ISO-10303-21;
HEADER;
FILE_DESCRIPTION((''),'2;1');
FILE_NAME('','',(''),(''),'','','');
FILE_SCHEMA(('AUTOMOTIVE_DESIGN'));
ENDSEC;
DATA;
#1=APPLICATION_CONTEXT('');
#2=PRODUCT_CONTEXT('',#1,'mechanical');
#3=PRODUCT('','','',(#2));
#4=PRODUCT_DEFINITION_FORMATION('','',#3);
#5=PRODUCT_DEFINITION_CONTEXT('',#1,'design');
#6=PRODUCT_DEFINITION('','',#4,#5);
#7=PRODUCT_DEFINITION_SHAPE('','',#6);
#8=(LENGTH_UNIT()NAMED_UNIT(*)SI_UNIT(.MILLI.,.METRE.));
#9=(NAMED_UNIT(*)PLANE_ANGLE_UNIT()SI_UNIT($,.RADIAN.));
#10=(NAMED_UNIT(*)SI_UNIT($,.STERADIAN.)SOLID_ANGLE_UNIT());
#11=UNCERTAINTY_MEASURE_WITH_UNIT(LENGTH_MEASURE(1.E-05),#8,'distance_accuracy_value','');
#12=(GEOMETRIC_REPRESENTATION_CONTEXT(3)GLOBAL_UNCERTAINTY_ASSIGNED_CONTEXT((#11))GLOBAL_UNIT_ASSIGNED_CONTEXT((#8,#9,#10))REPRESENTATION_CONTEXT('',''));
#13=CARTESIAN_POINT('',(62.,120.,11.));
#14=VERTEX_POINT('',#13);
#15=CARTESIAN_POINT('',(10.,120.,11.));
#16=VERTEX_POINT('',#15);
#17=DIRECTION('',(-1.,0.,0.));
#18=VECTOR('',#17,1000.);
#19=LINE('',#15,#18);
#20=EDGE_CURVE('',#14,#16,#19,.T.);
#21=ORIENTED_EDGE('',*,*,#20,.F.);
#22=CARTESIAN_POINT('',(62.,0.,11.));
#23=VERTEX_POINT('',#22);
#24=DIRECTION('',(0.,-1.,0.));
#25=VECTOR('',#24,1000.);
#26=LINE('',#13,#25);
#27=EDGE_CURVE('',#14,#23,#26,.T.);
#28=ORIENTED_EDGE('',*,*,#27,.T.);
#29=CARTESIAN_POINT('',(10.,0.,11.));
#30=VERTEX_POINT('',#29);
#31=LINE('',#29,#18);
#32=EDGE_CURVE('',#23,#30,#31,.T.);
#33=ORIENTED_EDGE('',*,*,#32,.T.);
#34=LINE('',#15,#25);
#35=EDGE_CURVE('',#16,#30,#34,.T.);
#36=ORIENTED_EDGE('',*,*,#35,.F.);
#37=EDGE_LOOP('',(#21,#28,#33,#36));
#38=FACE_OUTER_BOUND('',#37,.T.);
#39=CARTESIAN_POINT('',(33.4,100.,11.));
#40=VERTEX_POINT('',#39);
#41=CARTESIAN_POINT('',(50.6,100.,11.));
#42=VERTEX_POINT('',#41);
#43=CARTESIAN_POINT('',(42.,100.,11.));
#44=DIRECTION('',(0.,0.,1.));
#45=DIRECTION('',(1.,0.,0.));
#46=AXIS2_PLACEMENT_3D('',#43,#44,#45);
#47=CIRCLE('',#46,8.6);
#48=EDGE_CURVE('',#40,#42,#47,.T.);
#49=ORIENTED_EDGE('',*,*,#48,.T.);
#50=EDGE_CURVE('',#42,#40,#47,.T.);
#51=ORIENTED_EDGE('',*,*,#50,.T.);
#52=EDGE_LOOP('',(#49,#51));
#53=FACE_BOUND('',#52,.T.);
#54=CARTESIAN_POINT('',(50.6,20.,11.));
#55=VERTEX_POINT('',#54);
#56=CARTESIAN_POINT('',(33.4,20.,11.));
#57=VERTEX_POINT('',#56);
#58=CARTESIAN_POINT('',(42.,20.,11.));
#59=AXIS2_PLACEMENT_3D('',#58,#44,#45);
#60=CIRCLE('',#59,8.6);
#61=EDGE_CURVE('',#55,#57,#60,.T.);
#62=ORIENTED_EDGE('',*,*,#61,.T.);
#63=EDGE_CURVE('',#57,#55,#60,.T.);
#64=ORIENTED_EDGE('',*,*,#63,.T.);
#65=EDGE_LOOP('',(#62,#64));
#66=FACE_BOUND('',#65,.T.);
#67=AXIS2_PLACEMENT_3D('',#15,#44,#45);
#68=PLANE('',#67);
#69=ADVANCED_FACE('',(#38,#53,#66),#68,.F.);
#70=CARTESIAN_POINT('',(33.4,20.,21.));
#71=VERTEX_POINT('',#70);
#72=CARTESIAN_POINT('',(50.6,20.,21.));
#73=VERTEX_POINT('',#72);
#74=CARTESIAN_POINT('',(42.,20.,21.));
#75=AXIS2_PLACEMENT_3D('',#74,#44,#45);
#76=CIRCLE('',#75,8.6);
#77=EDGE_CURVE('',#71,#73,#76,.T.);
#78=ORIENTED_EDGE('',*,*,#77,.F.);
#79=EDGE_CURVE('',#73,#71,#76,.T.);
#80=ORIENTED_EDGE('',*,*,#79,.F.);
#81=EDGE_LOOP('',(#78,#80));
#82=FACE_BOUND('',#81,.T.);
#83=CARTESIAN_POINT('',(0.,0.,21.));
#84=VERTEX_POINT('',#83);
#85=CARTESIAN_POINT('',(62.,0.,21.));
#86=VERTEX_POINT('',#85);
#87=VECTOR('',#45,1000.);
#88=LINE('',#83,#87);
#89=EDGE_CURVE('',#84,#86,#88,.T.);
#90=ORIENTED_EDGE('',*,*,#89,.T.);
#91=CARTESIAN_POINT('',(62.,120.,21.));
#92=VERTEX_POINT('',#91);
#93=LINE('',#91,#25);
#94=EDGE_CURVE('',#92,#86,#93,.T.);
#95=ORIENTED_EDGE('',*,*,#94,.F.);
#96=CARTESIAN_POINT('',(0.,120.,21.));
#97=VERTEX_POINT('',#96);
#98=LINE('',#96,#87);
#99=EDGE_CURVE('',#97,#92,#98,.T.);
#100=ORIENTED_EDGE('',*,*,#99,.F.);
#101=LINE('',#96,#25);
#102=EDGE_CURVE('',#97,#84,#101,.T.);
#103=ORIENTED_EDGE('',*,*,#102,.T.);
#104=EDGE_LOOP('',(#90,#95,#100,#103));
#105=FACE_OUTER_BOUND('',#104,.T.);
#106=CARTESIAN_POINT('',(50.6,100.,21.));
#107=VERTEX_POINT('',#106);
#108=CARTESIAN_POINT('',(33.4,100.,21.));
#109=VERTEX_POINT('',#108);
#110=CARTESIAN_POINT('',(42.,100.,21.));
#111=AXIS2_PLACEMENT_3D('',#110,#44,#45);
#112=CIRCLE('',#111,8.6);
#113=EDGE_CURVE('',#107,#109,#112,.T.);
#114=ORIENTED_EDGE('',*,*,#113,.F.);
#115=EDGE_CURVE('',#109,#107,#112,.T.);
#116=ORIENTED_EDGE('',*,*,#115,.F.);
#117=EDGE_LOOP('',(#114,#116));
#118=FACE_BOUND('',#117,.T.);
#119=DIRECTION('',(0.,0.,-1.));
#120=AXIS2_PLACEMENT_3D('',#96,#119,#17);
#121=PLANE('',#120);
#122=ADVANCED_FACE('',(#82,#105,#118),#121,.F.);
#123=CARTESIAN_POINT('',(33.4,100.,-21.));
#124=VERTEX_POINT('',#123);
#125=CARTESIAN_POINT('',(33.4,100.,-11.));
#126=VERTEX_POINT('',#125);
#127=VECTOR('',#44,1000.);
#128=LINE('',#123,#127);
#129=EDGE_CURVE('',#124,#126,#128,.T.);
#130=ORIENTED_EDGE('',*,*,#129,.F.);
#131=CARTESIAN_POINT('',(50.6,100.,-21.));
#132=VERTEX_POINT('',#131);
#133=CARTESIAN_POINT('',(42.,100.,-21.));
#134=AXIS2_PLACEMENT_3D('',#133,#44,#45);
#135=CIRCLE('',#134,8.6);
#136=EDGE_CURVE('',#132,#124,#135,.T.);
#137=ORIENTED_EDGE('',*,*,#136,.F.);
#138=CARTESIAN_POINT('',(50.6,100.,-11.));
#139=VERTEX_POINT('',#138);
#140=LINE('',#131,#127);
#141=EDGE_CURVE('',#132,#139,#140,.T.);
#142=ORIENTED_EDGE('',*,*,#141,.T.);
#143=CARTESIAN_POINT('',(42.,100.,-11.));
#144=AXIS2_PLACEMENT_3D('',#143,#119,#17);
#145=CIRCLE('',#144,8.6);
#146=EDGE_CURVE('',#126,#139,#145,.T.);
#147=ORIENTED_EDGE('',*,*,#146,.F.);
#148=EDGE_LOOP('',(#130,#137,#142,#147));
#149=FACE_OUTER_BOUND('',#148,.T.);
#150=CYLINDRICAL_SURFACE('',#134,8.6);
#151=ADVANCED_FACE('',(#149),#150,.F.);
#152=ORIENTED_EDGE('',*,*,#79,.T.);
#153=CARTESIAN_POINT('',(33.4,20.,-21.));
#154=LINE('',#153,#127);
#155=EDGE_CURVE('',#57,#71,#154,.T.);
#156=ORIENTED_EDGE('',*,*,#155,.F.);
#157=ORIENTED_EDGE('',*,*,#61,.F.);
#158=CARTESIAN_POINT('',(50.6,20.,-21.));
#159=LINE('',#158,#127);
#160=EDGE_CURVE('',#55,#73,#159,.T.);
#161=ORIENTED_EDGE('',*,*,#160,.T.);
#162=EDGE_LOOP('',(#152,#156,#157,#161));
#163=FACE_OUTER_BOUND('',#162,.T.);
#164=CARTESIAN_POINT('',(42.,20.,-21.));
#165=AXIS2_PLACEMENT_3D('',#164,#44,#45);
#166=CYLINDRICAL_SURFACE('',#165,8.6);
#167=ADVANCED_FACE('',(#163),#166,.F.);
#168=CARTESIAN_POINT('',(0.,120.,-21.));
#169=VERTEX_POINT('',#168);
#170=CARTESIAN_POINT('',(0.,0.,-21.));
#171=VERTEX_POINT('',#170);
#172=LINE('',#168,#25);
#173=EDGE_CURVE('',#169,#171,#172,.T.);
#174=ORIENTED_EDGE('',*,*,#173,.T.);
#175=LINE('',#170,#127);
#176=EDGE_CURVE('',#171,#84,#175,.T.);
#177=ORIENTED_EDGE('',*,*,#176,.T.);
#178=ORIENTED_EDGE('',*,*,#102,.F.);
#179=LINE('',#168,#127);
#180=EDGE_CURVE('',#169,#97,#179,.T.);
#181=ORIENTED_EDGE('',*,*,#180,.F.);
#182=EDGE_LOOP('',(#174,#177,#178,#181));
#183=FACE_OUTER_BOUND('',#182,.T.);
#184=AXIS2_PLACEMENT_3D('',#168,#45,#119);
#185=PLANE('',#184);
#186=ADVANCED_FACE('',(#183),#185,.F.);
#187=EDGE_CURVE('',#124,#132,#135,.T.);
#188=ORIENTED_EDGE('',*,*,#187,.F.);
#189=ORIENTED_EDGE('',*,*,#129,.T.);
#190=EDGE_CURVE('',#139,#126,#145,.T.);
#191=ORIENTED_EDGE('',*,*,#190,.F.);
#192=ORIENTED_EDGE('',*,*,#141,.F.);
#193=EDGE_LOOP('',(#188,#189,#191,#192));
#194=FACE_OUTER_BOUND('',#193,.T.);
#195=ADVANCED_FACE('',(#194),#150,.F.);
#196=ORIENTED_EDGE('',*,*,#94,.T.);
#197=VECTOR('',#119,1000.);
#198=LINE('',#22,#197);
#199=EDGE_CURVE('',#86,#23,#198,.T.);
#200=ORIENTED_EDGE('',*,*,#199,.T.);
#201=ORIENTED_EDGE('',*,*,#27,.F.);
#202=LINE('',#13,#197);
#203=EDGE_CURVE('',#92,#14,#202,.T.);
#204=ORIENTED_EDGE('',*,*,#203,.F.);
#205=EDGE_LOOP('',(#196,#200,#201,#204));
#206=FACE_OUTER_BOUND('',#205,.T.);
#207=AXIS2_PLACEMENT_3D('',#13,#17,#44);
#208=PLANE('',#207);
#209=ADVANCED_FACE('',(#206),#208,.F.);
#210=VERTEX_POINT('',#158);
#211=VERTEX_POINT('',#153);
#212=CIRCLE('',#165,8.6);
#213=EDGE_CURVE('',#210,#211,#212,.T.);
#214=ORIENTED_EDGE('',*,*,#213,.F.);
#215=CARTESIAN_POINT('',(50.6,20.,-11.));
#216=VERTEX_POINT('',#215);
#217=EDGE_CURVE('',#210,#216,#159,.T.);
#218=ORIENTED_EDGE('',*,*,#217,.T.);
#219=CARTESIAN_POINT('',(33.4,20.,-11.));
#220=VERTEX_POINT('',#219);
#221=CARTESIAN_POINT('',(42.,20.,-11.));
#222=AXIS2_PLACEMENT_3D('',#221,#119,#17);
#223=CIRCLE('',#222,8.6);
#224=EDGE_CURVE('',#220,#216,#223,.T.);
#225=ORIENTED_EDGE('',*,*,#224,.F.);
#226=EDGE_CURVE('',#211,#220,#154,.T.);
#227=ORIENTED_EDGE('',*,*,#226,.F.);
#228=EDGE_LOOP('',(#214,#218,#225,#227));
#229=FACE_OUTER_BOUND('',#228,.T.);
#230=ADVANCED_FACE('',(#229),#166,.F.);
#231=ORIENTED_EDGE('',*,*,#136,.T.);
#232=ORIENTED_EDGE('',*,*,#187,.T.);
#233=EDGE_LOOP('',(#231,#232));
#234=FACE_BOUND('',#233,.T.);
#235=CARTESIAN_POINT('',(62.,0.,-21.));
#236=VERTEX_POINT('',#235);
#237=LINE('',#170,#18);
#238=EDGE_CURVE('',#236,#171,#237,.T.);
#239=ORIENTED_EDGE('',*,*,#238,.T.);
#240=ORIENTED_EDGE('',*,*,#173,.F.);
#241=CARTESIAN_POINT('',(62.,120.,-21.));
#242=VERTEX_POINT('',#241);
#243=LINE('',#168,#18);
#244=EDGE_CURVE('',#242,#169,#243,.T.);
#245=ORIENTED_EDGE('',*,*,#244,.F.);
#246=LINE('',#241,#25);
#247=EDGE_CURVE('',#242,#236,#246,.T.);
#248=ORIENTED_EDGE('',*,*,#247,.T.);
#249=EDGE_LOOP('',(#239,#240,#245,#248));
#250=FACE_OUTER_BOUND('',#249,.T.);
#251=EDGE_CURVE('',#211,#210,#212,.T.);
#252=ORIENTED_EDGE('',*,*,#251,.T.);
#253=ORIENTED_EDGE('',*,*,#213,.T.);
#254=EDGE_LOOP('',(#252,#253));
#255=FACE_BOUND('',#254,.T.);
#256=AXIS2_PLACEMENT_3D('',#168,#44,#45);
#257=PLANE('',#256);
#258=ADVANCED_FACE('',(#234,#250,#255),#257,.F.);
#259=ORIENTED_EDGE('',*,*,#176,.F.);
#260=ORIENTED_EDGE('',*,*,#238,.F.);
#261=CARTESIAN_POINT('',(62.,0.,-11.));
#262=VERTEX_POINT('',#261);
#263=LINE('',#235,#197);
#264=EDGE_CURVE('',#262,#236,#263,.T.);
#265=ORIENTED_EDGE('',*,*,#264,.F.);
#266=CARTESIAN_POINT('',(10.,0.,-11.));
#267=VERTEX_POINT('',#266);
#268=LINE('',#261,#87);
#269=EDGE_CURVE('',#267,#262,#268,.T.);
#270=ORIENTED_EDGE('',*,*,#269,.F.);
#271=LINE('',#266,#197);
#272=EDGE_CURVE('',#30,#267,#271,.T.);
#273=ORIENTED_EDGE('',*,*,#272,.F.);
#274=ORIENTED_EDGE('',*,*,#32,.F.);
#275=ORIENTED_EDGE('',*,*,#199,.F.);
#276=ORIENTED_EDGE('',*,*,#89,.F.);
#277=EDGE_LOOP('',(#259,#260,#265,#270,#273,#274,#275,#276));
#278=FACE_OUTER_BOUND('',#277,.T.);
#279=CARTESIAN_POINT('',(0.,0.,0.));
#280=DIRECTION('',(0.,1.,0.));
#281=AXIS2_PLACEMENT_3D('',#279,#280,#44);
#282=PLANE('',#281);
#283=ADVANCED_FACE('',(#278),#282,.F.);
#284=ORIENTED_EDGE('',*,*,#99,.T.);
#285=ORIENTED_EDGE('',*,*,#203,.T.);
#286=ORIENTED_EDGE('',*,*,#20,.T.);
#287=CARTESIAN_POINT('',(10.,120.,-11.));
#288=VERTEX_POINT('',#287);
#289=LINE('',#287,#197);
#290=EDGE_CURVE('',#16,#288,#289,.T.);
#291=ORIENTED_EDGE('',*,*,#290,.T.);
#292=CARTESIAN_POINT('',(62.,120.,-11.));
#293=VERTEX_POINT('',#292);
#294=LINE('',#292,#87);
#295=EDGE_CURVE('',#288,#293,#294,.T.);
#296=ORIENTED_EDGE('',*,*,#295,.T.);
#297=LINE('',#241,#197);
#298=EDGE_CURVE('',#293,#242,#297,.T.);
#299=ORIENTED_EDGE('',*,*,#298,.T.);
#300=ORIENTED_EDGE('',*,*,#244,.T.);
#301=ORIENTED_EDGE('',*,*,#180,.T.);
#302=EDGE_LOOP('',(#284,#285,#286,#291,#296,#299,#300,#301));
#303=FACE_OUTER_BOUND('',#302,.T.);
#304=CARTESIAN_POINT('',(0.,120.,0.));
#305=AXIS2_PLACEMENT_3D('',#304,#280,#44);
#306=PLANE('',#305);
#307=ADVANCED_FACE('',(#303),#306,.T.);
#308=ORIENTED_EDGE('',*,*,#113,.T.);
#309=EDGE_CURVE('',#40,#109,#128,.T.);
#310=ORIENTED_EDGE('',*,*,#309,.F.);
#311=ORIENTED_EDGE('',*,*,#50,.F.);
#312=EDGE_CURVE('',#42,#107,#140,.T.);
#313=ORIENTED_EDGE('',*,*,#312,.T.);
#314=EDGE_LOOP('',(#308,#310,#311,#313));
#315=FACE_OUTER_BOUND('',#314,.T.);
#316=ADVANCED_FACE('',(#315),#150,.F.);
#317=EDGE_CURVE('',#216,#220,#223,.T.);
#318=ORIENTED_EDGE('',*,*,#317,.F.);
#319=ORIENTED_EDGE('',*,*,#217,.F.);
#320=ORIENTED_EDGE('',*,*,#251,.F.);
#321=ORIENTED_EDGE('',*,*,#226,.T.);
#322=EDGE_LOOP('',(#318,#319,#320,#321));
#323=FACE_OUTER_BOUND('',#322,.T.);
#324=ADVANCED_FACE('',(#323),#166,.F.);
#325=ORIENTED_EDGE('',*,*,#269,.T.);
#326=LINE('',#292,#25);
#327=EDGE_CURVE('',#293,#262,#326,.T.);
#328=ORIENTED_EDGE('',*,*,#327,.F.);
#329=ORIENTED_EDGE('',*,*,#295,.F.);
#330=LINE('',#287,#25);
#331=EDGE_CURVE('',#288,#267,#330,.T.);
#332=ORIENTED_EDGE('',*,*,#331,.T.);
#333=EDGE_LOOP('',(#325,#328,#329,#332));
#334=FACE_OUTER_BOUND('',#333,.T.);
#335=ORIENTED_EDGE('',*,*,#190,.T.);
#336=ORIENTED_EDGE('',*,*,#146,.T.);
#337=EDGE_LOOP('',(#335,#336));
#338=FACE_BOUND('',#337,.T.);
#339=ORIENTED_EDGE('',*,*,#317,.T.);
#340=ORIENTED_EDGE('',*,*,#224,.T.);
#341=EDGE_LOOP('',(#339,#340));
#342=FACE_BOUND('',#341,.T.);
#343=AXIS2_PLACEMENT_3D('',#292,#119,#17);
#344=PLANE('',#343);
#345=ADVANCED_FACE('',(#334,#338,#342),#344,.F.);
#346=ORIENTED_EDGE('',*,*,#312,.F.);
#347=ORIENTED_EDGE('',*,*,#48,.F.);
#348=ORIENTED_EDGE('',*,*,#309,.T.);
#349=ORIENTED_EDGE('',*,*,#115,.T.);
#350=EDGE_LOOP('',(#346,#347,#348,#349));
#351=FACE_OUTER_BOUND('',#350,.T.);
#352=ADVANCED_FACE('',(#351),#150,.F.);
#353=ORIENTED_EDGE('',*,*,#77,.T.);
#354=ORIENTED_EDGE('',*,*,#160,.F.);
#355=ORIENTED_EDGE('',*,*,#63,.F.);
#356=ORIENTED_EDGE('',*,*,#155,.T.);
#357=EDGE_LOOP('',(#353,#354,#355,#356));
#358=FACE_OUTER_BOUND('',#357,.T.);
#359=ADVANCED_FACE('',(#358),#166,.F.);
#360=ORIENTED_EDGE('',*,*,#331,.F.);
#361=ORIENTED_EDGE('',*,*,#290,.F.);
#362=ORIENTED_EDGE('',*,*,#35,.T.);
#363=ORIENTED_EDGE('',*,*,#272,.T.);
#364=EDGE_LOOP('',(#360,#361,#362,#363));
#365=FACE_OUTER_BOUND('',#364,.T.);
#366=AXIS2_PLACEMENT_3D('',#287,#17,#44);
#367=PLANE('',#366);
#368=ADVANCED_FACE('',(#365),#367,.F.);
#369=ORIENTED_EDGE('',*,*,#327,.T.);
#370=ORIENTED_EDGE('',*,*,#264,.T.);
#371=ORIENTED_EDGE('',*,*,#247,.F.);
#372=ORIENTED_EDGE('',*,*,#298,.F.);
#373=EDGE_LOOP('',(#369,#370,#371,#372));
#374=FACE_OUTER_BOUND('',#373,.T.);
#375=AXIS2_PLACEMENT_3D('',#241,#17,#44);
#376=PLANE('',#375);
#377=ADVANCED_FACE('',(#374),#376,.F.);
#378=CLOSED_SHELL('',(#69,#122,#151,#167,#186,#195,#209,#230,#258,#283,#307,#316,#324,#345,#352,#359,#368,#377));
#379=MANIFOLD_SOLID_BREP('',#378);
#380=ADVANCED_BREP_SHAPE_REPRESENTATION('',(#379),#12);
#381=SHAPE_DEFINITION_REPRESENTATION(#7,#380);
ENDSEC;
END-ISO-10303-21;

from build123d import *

# Parameters (mm, degrees)
EXTRUDE_1_DEPTH     = 120
SKETCH_2_R          = 8.6
CUT_EXTRUDE_1_DEPTH = 142.449637681


with BuildPart() as part:
    # 草图1 → 凸台-拉伸1 (new body)
    with BuildSketch(Plane(origin=(0, 0, 0), x_dir=(1, 0, 0), z_dir=(0, 1, 0))):
        Polygon((62, 11), (10, 11), (10, -11), (62, -11), (62, -21), (0, -21), (0, 21), (62, 21), align=None)
    extrude(amount=EXTRUDE_1_DEPTH)

    # 草图2 → 切除-拉伸1 (cut, through all)
    with BuildSketch(Plane.XY.offset(21)):
        with Locations((42, 100)):
            Circle(SKETCH_2_R)
        with Locations((42, 20)):
            Circle(SKETCH_2_R)
    extrude(amount=-CUT_EXTRUDE_1_DEPTH, mode=Mode.SUBTRACT)


solid = part.part
